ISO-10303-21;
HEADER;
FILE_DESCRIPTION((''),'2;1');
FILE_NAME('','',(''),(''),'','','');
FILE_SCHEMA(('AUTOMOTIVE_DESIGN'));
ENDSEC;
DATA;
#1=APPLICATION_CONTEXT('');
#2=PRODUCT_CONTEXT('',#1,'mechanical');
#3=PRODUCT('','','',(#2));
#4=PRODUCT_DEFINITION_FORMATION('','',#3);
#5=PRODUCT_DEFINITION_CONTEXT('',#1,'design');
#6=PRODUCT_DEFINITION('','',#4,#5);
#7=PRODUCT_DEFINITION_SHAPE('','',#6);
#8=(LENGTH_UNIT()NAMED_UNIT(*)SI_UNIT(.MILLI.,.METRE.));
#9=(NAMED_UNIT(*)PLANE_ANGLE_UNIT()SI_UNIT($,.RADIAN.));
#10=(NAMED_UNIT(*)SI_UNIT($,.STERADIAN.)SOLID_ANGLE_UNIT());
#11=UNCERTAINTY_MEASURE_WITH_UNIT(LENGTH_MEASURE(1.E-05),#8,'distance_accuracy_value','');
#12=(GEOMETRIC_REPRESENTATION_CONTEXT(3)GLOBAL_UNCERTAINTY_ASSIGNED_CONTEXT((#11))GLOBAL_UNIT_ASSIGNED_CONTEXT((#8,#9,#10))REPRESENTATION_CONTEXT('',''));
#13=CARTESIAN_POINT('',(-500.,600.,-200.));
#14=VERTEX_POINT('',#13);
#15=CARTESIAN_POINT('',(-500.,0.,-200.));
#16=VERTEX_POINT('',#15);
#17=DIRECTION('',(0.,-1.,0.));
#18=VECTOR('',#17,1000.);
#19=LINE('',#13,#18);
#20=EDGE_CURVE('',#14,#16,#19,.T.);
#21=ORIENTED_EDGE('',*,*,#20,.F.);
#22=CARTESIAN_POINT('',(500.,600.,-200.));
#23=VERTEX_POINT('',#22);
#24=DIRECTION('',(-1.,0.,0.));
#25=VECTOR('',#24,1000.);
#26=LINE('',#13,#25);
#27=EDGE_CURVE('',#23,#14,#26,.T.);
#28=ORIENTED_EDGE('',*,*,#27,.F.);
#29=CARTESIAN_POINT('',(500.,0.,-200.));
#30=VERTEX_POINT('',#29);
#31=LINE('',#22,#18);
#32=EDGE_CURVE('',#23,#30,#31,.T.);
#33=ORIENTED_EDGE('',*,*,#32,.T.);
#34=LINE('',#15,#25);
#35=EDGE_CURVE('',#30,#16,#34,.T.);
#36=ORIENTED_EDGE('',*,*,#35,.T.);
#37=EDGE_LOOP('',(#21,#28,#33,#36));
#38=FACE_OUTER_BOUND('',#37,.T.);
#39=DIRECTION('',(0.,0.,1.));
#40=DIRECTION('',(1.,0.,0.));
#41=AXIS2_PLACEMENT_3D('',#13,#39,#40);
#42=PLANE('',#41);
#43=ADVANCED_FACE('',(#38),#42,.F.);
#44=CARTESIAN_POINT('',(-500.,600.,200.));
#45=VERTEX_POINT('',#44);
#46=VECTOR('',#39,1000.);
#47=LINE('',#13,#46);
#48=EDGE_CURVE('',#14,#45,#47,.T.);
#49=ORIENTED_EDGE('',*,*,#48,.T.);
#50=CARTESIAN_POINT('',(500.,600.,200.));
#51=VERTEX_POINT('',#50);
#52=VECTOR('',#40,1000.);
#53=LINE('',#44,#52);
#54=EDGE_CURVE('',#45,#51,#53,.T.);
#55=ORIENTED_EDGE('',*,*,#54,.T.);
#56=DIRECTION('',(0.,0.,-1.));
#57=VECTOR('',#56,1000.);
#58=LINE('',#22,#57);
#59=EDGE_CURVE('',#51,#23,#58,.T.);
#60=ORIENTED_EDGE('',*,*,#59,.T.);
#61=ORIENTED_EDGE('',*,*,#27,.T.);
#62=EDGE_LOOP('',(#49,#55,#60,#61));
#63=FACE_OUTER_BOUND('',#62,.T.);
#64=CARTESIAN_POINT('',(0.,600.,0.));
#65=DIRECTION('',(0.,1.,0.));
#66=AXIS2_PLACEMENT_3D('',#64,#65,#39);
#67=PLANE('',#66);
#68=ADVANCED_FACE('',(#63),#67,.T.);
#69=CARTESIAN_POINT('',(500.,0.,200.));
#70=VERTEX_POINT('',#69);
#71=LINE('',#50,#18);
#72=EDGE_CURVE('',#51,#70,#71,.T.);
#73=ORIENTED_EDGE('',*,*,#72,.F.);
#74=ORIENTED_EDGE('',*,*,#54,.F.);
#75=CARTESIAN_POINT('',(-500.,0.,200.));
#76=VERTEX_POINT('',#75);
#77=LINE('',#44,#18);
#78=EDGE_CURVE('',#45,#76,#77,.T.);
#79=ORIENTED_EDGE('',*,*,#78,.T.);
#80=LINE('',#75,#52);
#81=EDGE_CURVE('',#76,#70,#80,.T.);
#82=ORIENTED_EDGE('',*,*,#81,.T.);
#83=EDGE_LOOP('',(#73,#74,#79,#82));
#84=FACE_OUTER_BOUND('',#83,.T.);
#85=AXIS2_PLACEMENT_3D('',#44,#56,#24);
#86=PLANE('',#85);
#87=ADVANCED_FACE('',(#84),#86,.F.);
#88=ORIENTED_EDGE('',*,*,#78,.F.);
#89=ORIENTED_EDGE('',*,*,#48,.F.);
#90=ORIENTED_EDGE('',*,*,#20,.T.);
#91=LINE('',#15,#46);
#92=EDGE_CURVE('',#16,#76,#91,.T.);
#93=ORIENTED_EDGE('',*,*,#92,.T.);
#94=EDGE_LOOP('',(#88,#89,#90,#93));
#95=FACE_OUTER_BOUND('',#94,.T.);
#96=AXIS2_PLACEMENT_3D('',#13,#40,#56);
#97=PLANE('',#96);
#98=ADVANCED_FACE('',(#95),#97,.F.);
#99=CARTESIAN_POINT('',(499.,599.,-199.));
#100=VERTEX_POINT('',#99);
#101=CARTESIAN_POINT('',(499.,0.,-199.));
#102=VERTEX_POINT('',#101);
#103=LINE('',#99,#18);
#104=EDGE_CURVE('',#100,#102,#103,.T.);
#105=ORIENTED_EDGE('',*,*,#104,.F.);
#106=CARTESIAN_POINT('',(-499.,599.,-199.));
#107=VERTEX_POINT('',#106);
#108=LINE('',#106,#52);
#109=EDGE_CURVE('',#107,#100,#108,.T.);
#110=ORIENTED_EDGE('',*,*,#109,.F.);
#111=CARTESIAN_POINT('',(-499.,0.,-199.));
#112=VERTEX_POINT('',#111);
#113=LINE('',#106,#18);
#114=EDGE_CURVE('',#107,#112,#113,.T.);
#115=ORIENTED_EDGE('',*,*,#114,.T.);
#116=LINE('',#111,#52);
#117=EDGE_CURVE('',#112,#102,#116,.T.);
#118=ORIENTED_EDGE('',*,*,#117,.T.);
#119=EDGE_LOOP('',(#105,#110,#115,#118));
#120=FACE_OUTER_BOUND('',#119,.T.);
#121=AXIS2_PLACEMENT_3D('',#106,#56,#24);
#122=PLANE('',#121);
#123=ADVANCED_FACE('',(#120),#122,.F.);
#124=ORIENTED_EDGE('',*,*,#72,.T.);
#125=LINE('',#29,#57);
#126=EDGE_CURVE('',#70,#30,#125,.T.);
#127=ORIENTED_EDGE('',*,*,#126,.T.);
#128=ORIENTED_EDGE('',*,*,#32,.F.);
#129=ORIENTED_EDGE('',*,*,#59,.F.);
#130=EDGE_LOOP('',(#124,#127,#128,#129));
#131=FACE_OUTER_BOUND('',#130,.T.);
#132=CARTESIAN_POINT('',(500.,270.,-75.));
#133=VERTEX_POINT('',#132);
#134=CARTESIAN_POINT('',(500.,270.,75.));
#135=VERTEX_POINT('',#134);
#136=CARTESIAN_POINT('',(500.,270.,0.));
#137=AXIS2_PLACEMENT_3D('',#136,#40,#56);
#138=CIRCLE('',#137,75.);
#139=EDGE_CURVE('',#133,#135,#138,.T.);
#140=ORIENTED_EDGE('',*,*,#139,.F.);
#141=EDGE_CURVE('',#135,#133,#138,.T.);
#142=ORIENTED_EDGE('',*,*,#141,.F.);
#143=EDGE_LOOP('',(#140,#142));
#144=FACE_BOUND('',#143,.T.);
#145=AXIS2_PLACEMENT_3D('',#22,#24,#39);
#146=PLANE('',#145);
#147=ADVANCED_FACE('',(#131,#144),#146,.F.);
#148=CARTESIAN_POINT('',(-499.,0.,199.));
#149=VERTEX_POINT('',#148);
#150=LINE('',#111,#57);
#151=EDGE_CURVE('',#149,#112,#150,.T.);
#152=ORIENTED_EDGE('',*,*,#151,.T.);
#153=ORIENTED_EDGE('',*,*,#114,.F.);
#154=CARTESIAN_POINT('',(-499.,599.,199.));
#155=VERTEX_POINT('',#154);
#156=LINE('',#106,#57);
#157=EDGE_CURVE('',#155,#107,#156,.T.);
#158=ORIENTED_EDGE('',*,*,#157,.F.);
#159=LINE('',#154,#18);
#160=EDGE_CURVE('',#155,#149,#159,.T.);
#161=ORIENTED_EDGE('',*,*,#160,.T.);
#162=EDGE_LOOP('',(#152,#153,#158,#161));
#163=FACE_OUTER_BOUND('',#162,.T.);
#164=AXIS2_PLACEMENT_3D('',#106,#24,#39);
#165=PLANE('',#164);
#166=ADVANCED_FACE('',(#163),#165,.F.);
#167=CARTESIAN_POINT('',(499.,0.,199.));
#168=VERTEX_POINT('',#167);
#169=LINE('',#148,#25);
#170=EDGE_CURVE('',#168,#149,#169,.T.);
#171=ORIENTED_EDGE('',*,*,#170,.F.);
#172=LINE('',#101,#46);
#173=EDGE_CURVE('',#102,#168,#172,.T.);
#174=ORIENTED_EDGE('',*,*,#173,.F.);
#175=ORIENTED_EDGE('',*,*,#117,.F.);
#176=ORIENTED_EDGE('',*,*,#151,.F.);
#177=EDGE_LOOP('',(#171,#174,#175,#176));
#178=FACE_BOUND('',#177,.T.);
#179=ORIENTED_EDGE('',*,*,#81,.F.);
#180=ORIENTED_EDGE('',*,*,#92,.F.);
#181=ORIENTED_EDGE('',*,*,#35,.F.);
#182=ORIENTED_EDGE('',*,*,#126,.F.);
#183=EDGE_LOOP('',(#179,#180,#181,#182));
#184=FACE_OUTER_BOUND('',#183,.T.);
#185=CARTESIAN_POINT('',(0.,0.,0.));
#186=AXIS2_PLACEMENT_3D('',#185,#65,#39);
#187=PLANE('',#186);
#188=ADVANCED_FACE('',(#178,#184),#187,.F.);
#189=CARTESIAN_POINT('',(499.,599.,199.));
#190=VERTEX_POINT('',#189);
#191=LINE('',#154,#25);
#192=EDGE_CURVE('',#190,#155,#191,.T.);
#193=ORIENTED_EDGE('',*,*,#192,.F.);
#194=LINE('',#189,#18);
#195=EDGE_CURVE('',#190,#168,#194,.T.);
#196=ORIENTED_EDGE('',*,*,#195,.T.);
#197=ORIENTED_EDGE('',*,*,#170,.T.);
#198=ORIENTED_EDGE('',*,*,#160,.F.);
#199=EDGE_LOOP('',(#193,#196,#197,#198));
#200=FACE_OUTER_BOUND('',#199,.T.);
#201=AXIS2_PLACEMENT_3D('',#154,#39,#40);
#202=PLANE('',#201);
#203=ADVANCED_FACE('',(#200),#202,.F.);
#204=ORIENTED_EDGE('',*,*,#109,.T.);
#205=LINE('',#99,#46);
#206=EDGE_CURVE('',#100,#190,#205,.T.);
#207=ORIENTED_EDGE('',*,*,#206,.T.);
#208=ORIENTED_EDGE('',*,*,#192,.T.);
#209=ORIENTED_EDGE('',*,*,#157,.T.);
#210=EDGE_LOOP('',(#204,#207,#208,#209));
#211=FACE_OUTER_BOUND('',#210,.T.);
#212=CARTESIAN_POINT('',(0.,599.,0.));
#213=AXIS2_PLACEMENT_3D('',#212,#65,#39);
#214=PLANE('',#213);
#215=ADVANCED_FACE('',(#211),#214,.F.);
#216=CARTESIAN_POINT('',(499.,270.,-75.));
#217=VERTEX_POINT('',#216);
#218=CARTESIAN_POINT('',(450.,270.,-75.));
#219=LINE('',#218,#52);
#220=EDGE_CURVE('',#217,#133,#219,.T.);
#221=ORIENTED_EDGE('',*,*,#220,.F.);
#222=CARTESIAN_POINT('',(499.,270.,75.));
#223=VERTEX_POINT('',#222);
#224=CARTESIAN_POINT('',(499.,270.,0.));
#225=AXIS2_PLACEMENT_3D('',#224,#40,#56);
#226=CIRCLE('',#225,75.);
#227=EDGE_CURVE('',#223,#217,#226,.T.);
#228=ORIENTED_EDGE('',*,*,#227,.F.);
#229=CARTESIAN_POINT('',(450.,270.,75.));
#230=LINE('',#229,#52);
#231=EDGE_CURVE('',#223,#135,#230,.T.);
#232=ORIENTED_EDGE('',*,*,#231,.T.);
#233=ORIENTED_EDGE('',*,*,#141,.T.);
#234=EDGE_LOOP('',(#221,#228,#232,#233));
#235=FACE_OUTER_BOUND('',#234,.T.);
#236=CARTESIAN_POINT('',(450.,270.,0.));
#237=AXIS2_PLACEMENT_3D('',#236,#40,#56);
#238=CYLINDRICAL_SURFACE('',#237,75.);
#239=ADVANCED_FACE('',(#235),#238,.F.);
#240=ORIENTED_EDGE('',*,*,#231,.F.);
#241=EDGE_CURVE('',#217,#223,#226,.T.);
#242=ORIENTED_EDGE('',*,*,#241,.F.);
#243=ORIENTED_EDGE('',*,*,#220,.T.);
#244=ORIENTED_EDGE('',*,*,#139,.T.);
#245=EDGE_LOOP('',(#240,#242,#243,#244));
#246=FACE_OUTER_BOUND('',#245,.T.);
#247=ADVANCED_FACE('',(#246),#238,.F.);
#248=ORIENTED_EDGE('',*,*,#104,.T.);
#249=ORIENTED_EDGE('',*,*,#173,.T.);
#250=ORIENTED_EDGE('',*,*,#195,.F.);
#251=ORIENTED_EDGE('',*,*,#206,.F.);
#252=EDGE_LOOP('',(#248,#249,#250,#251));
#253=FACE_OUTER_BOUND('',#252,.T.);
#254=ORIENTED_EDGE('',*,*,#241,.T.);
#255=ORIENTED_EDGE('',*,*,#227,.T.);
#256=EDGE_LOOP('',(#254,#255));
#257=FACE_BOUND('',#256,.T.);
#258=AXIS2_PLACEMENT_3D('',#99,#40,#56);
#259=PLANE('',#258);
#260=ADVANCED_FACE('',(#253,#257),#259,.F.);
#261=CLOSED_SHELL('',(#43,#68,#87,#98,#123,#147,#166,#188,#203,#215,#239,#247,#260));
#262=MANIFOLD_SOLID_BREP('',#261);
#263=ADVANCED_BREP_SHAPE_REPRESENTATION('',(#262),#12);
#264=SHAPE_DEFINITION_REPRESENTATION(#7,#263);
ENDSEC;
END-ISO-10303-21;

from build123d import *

# Parameters (mm, degrees)
SKETCH1_W           = 1000
SKETCH1_H           = 400
BOSS_EXTRUDE1_DEPTH = 600
SKETCH2_W           = 998
SKETCH2_H           = 398
CUT_EXTRUDE1_DEPTH  = 599
SKETCH3_R           = 75
CUT_EXTRUDE2_DEPTH  = 50


with BuildPart() as part:
    # Sketch1 → Boss-Extrude1 (new body)
    with BuildSketch(Plane(origin=(0, 0, 0), x_dir=(1, 0, 0), z_dir=(0, 1, 0))):
        Rectangle(SKETCH1_W, SKETCH1_H)
    extrude(amount=BOSS_EXTRUDE1_DEPTH)

    # Sketch2 → Cut-Extrude1 (cut)
    with BuildSketch(Plane.XZ):
        Rectangle(SKETCH2_W, SKETCH2_H)
    extrude(amount=-CUT_EXTRUDE1_DEPTH, mode=Mode.SUBTRACT)

    # Sketch3 → Cut-Extrude2 (cut)
    with BuildSketch(Plane(origin=(500, 0, 0), x_dir=(0, 0, -1), z_dir=(1, 0, 0))):
        with Locations((0, 270)):
            Circle(SKETCH3_R)
    extrude(amount=-CUT_EXTRUDE2_DEPTH, mode=Mode.SUBTRACT)


solid = part.part
